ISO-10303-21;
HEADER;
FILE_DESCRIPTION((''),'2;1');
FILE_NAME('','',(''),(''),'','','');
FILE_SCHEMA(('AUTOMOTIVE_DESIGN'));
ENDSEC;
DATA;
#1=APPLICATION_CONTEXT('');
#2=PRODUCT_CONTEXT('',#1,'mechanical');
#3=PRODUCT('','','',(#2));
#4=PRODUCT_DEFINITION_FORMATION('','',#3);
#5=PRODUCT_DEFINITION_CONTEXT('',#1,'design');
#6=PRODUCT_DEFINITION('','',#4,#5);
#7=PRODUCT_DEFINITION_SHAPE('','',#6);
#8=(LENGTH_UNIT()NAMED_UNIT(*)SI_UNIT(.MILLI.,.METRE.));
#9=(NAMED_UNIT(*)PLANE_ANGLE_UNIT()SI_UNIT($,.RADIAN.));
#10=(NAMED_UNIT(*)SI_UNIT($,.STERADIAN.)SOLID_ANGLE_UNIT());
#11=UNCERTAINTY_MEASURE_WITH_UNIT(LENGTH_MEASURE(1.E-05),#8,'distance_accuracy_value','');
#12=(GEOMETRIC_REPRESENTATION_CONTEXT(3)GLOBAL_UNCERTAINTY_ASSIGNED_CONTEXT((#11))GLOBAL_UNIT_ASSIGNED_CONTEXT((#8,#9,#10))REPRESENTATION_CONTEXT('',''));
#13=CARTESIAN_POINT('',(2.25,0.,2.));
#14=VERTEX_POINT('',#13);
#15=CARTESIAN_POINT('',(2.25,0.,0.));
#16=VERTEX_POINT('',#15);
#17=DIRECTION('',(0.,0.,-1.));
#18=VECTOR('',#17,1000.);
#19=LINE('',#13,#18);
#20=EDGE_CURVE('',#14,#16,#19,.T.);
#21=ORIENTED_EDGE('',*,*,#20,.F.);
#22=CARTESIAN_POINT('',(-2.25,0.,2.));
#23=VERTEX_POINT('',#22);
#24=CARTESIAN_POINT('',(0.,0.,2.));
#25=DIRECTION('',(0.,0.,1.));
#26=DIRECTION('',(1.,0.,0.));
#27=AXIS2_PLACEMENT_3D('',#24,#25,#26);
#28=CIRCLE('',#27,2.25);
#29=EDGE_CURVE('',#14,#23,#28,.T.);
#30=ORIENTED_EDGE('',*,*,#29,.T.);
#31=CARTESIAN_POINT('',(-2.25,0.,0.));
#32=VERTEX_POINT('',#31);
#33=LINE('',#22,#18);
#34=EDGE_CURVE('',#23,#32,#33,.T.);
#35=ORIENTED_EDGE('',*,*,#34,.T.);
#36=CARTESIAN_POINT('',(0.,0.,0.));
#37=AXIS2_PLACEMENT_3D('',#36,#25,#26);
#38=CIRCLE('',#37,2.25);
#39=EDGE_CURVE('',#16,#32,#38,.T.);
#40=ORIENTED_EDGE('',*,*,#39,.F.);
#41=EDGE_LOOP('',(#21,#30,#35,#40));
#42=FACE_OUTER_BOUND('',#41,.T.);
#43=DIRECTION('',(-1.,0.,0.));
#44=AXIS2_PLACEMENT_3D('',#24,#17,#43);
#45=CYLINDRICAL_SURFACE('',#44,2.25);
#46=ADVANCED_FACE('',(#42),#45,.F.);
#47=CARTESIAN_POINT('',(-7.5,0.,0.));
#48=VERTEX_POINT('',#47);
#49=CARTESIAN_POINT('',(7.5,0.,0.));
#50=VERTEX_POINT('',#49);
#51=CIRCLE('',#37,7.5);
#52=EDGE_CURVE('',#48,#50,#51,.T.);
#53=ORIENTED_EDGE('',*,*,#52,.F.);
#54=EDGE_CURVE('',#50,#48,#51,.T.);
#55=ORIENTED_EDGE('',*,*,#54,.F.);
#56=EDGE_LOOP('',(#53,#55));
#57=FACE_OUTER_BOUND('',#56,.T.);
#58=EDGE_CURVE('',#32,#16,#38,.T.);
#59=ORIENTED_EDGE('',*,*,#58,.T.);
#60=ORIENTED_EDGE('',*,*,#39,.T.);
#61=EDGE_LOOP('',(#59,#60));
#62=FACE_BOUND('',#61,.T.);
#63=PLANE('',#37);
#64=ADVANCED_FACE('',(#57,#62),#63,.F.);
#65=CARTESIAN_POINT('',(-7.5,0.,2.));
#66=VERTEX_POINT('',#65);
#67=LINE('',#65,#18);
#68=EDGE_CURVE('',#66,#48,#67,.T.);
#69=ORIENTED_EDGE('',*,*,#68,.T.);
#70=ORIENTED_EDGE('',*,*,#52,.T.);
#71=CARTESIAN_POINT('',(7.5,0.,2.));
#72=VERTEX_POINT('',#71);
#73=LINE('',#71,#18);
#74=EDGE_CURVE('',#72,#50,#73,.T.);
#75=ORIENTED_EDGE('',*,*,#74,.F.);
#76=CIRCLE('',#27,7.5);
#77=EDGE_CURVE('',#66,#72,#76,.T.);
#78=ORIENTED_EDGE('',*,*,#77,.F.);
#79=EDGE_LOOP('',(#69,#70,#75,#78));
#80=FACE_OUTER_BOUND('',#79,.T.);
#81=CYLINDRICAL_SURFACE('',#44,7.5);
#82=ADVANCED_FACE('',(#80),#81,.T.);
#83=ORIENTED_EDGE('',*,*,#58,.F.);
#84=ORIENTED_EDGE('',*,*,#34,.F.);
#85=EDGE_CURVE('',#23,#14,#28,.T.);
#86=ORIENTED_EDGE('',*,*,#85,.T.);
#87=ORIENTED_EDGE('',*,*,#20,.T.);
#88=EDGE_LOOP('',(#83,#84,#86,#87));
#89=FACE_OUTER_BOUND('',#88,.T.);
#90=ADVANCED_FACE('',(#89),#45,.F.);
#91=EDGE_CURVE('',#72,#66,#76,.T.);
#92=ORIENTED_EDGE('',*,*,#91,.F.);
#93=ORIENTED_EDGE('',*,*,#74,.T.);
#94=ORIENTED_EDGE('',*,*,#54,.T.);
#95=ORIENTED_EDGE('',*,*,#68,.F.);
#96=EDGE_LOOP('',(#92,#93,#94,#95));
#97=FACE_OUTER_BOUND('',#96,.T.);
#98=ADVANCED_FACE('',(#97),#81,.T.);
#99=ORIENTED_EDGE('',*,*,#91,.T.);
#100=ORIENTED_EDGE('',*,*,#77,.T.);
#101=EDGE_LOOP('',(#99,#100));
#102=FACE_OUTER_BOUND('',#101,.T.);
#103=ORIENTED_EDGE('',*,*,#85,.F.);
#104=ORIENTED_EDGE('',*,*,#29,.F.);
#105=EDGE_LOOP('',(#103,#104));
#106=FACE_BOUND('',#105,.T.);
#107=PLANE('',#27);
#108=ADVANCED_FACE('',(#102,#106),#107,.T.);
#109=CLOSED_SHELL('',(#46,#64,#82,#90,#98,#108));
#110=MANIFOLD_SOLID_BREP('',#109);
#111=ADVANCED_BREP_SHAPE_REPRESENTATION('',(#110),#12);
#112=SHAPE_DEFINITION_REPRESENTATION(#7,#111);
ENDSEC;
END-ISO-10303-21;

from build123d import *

# Parameters (mm, degrees)
SKETCH_1_R      = 7.5
SKETCH_1_R_2    = 2.25
EXTRUDE_1_DEPTH = 2


with BuildPart() as part:
    # 草图1 → 凸台-拉伸1 (new body)
    with BuildSketch(Plane.XY):
        Circle(SKETCH_1_R)
        Circle(SKETCH_1_R_2, mode=Mode.SUBTRACT)
    extrude(amount=EXTRUDE_1_DEPTH)


solid = part.part
